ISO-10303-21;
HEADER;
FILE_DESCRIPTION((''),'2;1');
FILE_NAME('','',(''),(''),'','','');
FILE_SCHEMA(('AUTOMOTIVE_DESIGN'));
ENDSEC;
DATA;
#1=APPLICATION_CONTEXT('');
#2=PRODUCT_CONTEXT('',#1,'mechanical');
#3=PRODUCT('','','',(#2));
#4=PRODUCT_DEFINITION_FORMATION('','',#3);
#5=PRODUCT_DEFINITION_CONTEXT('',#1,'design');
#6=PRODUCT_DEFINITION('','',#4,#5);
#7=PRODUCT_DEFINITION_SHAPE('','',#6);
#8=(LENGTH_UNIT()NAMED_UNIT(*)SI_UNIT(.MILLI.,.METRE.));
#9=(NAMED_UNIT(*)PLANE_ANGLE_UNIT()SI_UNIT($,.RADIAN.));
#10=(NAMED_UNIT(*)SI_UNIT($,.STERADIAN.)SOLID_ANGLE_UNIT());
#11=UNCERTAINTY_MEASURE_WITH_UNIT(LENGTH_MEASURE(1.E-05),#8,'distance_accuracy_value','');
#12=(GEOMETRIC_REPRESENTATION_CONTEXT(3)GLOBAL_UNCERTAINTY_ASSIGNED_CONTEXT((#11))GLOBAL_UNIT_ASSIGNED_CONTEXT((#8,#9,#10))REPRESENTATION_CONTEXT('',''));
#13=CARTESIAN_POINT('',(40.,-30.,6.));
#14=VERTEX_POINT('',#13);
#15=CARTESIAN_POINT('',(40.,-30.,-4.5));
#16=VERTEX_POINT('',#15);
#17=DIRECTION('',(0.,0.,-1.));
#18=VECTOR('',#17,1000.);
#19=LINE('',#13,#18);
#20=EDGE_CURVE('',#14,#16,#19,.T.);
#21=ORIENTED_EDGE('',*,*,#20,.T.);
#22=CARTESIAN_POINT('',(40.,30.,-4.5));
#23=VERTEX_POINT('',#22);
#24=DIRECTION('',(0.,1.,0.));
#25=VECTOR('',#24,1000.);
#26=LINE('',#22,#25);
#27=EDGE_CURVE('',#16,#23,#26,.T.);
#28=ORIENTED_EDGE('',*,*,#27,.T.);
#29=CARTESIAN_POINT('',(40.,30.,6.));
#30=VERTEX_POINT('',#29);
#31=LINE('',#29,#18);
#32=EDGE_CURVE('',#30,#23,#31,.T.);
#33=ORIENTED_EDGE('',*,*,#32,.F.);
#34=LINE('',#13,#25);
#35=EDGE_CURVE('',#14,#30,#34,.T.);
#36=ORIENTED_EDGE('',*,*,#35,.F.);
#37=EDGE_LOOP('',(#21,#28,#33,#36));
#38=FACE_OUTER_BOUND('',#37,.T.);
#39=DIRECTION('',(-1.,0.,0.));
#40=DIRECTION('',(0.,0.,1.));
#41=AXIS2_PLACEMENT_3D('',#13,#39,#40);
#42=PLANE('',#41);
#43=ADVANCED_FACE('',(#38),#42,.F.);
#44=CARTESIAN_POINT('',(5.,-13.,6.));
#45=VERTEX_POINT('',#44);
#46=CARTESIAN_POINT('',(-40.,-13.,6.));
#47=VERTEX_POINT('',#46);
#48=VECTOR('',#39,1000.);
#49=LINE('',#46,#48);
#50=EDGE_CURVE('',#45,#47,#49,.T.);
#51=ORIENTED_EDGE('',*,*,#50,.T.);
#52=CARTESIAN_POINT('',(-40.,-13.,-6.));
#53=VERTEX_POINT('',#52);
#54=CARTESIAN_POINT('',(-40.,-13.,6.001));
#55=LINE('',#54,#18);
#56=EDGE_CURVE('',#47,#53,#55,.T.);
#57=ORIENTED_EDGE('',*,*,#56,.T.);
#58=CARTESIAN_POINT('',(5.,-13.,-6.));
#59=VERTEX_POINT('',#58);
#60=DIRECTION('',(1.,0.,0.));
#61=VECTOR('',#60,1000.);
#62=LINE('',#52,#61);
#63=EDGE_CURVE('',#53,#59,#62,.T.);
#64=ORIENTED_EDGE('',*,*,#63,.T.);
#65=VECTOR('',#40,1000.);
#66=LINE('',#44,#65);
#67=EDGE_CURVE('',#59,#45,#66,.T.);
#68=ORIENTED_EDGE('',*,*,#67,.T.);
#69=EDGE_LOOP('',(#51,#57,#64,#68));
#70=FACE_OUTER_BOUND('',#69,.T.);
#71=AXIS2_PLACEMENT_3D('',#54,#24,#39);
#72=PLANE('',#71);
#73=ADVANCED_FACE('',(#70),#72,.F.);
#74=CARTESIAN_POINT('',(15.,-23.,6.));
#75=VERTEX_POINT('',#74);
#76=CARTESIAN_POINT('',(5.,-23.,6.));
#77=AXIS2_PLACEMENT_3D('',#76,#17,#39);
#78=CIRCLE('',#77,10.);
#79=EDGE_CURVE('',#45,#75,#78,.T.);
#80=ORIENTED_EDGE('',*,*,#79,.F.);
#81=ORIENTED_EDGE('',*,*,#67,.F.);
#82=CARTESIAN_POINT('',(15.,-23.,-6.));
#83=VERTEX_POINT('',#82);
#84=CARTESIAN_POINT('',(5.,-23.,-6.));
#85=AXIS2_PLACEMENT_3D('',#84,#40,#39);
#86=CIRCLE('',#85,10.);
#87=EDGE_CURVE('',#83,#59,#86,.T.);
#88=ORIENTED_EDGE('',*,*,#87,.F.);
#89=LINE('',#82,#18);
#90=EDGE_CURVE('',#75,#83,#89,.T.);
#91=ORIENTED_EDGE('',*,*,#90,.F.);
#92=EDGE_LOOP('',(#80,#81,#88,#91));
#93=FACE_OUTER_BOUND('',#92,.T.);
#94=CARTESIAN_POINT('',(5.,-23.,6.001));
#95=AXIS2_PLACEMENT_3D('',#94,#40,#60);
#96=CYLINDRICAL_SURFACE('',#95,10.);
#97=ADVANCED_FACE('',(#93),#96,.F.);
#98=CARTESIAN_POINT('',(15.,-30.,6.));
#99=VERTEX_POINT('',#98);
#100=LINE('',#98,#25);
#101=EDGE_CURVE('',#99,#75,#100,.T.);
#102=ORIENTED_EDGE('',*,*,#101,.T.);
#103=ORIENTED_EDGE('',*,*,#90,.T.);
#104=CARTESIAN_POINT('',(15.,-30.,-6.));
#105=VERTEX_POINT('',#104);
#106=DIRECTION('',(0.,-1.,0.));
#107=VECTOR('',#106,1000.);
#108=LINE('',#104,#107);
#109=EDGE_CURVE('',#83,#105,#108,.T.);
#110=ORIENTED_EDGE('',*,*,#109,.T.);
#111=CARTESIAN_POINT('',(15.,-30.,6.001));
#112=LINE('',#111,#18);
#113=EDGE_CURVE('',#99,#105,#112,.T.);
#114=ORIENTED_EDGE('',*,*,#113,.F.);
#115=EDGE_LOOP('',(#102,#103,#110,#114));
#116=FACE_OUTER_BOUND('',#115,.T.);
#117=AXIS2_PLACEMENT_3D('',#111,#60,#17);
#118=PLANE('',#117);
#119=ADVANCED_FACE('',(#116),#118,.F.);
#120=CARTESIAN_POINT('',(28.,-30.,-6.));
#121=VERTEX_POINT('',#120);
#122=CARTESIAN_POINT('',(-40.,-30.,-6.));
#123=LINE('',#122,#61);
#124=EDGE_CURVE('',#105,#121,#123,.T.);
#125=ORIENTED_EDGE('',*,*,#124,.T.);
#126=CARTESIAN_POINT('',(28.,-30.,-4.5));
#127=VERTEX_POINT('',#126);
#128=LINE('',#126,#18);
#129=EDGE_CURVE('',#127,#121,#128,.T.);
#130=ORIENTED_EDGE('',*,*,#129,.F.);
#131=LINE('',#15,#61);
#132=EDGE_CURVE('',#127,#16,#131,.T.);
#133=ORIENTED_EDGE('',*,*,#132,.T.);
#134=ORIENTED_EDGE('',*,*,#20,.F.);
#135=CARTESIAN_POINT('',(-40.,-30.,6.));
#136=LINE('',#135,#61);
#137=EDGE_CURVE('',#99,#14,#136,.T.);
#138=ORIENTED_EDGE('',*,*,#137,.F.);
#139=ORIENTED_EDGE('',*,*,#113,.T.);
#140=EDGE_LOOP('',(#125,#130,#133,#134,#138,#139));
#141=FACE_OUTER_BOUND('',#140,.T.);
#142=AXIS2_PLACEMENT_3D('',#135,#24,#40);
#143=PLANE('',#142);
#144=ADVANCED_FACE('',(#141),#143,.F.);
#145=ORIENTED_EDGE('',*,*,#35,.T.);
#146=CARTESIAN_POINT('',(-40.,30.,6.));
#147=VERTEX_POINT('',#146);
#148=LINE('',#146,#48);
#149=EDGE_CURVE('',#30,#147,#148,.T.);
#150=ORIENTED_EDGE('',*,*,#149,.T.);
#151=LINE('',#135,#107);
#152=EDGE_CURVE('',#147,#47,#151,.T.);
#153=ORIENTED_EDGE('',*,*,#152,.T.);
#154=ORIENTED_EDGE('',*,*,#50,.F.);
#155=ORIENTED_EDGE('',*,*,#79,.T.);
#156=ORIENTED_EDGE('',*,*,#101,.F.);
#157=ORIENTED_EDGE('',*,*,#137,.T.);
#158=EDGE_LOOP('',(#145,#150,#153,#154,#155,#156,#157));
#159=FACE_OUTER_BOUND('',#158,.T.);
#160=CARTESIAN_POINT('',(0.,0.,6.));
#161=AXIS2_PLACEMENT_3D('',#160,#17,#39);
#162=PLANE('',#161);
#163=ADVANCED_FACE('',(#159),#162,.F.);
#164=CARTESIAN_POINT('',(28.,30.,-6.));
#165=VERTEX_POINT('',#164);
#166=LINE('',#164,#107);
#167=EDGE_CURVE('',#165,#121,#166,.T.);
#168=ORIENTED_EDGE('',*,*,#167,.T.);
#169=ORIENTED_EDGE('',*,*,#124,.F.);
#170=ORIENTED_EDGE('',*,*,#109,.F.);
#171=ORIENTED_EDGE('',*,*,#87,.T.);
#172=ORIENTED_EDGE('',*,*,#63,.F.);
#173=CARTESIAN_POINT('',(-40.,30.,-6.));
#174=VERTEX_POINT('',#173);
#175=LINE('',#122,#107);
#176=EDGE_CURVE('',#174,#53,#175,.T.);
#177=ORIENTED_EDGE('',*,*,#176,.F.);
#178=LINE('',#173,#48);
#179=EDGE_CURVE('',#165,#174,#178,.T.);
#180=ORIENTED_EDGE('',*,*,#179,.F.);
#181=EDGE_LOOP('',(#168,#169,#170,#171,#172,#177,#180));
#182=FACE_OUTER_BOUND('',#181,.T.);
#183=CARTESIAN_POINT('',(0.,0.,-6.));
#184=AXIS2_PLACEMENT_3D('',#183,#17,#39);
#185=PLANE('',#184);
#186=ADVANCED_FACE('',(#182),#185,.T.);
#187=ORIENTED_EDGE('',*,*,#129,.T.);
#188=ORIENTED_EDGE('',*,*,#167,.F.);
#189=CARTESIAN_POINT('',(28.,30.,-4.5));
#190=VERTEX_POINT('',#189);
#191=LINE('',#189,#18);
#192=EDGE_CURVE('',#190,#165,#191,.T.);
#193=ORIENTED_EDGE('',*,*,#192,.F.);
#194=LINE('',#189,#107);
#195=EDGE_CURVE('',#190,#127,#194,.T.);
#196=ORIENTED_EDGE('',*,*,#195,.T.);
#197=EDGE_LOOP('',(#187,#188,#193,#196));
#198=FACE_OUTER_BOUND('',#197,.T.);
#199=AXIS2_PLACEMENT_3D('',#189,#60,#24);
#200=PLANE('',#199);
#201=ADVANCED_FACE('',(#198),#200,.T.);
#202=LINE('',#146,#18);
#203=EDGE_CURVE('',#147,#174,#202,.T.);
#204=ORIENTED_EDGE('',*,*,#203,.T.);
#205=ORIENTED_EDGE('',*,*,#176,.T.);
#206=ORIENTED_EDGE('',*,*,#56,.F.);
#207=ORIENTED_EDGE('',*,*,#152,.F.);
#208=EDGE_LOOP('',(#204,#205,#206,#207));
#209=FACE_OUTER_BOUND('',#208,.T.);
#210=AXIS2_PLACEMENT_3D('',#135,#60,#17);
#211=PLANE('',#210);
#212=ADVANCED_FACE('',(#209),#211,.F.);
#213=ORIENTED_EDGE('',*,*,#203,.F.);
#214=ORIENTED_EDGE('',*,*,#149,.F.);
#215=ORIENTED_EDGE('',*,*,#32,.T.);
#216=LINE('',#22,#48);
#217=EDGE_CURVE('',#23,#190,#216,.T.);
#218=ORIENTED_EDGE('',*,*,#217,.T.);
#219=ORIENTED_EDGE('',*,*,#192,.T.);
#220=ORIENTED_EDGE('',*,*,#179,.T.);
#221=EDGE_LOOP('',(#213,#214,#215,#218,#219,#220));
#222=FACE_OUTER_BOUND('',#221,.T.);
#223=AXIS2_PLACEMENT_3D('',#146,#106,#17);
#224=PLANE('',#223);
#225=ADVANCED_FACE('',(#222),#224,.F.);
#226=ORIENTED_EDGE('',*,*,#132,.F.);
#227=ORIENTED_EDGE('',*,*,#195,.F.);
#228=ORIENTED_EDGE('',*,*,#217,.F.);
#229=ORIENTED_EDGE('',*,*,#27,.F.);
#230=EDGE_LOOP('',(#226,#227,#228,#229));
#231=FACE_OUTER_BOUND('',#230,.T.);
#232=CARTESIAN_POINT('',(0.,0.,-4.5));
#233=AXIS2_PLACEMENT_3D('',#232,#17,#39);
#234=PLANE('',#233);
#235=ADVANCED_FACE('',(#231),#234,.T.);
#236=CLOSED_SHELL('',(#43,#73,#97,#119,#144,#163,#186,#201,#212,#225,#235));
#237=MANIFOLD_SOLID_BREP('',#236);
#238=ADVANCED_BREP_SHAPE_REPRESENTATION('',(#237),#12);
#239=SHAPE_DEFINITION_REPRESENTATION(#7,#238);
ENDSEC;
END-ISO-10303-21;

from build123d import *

# Parameters (mm, degrees)
SKETCH_1_W          = 80
SKETCH_1_H          = 60
EXTRUDE_1_DEPTH     = 6
SKETCH_2_W          = 12
SKETCH_2_H          = 60
CUT_EXTRUDE_1_DEPTH = 1.5
CUT_EXTRUDE_2_REACH = 53.42
SKETCH_3_W          = 55
SKETCH_3_H          = 17
FILLET_1_R          = 10


with BuildPart() as part:
    # 草图1 → 凸台-拉伸1 (new, symmetric)
    with BuildSketch(Plane.XY):
        Rectangle(SKETCH_1_W, SKETCH_1_H)
    extrude(amount=EXTRUDE_1_DEPTH, both=True)

    # 草图2 → 切除-拉伸1 (cut)
    with BuildSketch(Plane.XY.offset(-6)):
        with Locations((34, 0)):
            Rectangle(SKETCH_2_W, SKETCH_2_H)
    extrude(amount=CUT_EXTRUDE_1_DEPTH, mode=Mode.SUBTRACT)

    # 草图3 → 切除-拉伸2 (cut, up to next)
    with BuildSketch(Plane(origin=(0, 0, -6), x_dir=(-1, 0, 0), z_dir=(0, 0, -1)), mode=Mode.PRIVATE) as cut_extrude_2_sk1:
        with Locations((12.5, -21.5)):
            Rectangle(SKETCH_3_W, SKETCH_3_H)
    cut_extrude_2_tool1 = extrude(cut_extrude_2_sk1.sketch, amount=-CUT_EXTRUDE_2_REACH, mode=Mode.PRIVATE) & part.part
    add(cut_extrude_2_tool1.solids().sort_by_distance((-12.5, -21.5, -6))[0], mode=Mode.SUBTRACT)

    # 圆角1
    fillet_1_edges = [part.edges().sort_by_distance(p)[0] for p in [
        (15, -13, 0),
    ]]
    fillet(fillet_1_edges, radius=FILLET_1_R)


solid = part.part
